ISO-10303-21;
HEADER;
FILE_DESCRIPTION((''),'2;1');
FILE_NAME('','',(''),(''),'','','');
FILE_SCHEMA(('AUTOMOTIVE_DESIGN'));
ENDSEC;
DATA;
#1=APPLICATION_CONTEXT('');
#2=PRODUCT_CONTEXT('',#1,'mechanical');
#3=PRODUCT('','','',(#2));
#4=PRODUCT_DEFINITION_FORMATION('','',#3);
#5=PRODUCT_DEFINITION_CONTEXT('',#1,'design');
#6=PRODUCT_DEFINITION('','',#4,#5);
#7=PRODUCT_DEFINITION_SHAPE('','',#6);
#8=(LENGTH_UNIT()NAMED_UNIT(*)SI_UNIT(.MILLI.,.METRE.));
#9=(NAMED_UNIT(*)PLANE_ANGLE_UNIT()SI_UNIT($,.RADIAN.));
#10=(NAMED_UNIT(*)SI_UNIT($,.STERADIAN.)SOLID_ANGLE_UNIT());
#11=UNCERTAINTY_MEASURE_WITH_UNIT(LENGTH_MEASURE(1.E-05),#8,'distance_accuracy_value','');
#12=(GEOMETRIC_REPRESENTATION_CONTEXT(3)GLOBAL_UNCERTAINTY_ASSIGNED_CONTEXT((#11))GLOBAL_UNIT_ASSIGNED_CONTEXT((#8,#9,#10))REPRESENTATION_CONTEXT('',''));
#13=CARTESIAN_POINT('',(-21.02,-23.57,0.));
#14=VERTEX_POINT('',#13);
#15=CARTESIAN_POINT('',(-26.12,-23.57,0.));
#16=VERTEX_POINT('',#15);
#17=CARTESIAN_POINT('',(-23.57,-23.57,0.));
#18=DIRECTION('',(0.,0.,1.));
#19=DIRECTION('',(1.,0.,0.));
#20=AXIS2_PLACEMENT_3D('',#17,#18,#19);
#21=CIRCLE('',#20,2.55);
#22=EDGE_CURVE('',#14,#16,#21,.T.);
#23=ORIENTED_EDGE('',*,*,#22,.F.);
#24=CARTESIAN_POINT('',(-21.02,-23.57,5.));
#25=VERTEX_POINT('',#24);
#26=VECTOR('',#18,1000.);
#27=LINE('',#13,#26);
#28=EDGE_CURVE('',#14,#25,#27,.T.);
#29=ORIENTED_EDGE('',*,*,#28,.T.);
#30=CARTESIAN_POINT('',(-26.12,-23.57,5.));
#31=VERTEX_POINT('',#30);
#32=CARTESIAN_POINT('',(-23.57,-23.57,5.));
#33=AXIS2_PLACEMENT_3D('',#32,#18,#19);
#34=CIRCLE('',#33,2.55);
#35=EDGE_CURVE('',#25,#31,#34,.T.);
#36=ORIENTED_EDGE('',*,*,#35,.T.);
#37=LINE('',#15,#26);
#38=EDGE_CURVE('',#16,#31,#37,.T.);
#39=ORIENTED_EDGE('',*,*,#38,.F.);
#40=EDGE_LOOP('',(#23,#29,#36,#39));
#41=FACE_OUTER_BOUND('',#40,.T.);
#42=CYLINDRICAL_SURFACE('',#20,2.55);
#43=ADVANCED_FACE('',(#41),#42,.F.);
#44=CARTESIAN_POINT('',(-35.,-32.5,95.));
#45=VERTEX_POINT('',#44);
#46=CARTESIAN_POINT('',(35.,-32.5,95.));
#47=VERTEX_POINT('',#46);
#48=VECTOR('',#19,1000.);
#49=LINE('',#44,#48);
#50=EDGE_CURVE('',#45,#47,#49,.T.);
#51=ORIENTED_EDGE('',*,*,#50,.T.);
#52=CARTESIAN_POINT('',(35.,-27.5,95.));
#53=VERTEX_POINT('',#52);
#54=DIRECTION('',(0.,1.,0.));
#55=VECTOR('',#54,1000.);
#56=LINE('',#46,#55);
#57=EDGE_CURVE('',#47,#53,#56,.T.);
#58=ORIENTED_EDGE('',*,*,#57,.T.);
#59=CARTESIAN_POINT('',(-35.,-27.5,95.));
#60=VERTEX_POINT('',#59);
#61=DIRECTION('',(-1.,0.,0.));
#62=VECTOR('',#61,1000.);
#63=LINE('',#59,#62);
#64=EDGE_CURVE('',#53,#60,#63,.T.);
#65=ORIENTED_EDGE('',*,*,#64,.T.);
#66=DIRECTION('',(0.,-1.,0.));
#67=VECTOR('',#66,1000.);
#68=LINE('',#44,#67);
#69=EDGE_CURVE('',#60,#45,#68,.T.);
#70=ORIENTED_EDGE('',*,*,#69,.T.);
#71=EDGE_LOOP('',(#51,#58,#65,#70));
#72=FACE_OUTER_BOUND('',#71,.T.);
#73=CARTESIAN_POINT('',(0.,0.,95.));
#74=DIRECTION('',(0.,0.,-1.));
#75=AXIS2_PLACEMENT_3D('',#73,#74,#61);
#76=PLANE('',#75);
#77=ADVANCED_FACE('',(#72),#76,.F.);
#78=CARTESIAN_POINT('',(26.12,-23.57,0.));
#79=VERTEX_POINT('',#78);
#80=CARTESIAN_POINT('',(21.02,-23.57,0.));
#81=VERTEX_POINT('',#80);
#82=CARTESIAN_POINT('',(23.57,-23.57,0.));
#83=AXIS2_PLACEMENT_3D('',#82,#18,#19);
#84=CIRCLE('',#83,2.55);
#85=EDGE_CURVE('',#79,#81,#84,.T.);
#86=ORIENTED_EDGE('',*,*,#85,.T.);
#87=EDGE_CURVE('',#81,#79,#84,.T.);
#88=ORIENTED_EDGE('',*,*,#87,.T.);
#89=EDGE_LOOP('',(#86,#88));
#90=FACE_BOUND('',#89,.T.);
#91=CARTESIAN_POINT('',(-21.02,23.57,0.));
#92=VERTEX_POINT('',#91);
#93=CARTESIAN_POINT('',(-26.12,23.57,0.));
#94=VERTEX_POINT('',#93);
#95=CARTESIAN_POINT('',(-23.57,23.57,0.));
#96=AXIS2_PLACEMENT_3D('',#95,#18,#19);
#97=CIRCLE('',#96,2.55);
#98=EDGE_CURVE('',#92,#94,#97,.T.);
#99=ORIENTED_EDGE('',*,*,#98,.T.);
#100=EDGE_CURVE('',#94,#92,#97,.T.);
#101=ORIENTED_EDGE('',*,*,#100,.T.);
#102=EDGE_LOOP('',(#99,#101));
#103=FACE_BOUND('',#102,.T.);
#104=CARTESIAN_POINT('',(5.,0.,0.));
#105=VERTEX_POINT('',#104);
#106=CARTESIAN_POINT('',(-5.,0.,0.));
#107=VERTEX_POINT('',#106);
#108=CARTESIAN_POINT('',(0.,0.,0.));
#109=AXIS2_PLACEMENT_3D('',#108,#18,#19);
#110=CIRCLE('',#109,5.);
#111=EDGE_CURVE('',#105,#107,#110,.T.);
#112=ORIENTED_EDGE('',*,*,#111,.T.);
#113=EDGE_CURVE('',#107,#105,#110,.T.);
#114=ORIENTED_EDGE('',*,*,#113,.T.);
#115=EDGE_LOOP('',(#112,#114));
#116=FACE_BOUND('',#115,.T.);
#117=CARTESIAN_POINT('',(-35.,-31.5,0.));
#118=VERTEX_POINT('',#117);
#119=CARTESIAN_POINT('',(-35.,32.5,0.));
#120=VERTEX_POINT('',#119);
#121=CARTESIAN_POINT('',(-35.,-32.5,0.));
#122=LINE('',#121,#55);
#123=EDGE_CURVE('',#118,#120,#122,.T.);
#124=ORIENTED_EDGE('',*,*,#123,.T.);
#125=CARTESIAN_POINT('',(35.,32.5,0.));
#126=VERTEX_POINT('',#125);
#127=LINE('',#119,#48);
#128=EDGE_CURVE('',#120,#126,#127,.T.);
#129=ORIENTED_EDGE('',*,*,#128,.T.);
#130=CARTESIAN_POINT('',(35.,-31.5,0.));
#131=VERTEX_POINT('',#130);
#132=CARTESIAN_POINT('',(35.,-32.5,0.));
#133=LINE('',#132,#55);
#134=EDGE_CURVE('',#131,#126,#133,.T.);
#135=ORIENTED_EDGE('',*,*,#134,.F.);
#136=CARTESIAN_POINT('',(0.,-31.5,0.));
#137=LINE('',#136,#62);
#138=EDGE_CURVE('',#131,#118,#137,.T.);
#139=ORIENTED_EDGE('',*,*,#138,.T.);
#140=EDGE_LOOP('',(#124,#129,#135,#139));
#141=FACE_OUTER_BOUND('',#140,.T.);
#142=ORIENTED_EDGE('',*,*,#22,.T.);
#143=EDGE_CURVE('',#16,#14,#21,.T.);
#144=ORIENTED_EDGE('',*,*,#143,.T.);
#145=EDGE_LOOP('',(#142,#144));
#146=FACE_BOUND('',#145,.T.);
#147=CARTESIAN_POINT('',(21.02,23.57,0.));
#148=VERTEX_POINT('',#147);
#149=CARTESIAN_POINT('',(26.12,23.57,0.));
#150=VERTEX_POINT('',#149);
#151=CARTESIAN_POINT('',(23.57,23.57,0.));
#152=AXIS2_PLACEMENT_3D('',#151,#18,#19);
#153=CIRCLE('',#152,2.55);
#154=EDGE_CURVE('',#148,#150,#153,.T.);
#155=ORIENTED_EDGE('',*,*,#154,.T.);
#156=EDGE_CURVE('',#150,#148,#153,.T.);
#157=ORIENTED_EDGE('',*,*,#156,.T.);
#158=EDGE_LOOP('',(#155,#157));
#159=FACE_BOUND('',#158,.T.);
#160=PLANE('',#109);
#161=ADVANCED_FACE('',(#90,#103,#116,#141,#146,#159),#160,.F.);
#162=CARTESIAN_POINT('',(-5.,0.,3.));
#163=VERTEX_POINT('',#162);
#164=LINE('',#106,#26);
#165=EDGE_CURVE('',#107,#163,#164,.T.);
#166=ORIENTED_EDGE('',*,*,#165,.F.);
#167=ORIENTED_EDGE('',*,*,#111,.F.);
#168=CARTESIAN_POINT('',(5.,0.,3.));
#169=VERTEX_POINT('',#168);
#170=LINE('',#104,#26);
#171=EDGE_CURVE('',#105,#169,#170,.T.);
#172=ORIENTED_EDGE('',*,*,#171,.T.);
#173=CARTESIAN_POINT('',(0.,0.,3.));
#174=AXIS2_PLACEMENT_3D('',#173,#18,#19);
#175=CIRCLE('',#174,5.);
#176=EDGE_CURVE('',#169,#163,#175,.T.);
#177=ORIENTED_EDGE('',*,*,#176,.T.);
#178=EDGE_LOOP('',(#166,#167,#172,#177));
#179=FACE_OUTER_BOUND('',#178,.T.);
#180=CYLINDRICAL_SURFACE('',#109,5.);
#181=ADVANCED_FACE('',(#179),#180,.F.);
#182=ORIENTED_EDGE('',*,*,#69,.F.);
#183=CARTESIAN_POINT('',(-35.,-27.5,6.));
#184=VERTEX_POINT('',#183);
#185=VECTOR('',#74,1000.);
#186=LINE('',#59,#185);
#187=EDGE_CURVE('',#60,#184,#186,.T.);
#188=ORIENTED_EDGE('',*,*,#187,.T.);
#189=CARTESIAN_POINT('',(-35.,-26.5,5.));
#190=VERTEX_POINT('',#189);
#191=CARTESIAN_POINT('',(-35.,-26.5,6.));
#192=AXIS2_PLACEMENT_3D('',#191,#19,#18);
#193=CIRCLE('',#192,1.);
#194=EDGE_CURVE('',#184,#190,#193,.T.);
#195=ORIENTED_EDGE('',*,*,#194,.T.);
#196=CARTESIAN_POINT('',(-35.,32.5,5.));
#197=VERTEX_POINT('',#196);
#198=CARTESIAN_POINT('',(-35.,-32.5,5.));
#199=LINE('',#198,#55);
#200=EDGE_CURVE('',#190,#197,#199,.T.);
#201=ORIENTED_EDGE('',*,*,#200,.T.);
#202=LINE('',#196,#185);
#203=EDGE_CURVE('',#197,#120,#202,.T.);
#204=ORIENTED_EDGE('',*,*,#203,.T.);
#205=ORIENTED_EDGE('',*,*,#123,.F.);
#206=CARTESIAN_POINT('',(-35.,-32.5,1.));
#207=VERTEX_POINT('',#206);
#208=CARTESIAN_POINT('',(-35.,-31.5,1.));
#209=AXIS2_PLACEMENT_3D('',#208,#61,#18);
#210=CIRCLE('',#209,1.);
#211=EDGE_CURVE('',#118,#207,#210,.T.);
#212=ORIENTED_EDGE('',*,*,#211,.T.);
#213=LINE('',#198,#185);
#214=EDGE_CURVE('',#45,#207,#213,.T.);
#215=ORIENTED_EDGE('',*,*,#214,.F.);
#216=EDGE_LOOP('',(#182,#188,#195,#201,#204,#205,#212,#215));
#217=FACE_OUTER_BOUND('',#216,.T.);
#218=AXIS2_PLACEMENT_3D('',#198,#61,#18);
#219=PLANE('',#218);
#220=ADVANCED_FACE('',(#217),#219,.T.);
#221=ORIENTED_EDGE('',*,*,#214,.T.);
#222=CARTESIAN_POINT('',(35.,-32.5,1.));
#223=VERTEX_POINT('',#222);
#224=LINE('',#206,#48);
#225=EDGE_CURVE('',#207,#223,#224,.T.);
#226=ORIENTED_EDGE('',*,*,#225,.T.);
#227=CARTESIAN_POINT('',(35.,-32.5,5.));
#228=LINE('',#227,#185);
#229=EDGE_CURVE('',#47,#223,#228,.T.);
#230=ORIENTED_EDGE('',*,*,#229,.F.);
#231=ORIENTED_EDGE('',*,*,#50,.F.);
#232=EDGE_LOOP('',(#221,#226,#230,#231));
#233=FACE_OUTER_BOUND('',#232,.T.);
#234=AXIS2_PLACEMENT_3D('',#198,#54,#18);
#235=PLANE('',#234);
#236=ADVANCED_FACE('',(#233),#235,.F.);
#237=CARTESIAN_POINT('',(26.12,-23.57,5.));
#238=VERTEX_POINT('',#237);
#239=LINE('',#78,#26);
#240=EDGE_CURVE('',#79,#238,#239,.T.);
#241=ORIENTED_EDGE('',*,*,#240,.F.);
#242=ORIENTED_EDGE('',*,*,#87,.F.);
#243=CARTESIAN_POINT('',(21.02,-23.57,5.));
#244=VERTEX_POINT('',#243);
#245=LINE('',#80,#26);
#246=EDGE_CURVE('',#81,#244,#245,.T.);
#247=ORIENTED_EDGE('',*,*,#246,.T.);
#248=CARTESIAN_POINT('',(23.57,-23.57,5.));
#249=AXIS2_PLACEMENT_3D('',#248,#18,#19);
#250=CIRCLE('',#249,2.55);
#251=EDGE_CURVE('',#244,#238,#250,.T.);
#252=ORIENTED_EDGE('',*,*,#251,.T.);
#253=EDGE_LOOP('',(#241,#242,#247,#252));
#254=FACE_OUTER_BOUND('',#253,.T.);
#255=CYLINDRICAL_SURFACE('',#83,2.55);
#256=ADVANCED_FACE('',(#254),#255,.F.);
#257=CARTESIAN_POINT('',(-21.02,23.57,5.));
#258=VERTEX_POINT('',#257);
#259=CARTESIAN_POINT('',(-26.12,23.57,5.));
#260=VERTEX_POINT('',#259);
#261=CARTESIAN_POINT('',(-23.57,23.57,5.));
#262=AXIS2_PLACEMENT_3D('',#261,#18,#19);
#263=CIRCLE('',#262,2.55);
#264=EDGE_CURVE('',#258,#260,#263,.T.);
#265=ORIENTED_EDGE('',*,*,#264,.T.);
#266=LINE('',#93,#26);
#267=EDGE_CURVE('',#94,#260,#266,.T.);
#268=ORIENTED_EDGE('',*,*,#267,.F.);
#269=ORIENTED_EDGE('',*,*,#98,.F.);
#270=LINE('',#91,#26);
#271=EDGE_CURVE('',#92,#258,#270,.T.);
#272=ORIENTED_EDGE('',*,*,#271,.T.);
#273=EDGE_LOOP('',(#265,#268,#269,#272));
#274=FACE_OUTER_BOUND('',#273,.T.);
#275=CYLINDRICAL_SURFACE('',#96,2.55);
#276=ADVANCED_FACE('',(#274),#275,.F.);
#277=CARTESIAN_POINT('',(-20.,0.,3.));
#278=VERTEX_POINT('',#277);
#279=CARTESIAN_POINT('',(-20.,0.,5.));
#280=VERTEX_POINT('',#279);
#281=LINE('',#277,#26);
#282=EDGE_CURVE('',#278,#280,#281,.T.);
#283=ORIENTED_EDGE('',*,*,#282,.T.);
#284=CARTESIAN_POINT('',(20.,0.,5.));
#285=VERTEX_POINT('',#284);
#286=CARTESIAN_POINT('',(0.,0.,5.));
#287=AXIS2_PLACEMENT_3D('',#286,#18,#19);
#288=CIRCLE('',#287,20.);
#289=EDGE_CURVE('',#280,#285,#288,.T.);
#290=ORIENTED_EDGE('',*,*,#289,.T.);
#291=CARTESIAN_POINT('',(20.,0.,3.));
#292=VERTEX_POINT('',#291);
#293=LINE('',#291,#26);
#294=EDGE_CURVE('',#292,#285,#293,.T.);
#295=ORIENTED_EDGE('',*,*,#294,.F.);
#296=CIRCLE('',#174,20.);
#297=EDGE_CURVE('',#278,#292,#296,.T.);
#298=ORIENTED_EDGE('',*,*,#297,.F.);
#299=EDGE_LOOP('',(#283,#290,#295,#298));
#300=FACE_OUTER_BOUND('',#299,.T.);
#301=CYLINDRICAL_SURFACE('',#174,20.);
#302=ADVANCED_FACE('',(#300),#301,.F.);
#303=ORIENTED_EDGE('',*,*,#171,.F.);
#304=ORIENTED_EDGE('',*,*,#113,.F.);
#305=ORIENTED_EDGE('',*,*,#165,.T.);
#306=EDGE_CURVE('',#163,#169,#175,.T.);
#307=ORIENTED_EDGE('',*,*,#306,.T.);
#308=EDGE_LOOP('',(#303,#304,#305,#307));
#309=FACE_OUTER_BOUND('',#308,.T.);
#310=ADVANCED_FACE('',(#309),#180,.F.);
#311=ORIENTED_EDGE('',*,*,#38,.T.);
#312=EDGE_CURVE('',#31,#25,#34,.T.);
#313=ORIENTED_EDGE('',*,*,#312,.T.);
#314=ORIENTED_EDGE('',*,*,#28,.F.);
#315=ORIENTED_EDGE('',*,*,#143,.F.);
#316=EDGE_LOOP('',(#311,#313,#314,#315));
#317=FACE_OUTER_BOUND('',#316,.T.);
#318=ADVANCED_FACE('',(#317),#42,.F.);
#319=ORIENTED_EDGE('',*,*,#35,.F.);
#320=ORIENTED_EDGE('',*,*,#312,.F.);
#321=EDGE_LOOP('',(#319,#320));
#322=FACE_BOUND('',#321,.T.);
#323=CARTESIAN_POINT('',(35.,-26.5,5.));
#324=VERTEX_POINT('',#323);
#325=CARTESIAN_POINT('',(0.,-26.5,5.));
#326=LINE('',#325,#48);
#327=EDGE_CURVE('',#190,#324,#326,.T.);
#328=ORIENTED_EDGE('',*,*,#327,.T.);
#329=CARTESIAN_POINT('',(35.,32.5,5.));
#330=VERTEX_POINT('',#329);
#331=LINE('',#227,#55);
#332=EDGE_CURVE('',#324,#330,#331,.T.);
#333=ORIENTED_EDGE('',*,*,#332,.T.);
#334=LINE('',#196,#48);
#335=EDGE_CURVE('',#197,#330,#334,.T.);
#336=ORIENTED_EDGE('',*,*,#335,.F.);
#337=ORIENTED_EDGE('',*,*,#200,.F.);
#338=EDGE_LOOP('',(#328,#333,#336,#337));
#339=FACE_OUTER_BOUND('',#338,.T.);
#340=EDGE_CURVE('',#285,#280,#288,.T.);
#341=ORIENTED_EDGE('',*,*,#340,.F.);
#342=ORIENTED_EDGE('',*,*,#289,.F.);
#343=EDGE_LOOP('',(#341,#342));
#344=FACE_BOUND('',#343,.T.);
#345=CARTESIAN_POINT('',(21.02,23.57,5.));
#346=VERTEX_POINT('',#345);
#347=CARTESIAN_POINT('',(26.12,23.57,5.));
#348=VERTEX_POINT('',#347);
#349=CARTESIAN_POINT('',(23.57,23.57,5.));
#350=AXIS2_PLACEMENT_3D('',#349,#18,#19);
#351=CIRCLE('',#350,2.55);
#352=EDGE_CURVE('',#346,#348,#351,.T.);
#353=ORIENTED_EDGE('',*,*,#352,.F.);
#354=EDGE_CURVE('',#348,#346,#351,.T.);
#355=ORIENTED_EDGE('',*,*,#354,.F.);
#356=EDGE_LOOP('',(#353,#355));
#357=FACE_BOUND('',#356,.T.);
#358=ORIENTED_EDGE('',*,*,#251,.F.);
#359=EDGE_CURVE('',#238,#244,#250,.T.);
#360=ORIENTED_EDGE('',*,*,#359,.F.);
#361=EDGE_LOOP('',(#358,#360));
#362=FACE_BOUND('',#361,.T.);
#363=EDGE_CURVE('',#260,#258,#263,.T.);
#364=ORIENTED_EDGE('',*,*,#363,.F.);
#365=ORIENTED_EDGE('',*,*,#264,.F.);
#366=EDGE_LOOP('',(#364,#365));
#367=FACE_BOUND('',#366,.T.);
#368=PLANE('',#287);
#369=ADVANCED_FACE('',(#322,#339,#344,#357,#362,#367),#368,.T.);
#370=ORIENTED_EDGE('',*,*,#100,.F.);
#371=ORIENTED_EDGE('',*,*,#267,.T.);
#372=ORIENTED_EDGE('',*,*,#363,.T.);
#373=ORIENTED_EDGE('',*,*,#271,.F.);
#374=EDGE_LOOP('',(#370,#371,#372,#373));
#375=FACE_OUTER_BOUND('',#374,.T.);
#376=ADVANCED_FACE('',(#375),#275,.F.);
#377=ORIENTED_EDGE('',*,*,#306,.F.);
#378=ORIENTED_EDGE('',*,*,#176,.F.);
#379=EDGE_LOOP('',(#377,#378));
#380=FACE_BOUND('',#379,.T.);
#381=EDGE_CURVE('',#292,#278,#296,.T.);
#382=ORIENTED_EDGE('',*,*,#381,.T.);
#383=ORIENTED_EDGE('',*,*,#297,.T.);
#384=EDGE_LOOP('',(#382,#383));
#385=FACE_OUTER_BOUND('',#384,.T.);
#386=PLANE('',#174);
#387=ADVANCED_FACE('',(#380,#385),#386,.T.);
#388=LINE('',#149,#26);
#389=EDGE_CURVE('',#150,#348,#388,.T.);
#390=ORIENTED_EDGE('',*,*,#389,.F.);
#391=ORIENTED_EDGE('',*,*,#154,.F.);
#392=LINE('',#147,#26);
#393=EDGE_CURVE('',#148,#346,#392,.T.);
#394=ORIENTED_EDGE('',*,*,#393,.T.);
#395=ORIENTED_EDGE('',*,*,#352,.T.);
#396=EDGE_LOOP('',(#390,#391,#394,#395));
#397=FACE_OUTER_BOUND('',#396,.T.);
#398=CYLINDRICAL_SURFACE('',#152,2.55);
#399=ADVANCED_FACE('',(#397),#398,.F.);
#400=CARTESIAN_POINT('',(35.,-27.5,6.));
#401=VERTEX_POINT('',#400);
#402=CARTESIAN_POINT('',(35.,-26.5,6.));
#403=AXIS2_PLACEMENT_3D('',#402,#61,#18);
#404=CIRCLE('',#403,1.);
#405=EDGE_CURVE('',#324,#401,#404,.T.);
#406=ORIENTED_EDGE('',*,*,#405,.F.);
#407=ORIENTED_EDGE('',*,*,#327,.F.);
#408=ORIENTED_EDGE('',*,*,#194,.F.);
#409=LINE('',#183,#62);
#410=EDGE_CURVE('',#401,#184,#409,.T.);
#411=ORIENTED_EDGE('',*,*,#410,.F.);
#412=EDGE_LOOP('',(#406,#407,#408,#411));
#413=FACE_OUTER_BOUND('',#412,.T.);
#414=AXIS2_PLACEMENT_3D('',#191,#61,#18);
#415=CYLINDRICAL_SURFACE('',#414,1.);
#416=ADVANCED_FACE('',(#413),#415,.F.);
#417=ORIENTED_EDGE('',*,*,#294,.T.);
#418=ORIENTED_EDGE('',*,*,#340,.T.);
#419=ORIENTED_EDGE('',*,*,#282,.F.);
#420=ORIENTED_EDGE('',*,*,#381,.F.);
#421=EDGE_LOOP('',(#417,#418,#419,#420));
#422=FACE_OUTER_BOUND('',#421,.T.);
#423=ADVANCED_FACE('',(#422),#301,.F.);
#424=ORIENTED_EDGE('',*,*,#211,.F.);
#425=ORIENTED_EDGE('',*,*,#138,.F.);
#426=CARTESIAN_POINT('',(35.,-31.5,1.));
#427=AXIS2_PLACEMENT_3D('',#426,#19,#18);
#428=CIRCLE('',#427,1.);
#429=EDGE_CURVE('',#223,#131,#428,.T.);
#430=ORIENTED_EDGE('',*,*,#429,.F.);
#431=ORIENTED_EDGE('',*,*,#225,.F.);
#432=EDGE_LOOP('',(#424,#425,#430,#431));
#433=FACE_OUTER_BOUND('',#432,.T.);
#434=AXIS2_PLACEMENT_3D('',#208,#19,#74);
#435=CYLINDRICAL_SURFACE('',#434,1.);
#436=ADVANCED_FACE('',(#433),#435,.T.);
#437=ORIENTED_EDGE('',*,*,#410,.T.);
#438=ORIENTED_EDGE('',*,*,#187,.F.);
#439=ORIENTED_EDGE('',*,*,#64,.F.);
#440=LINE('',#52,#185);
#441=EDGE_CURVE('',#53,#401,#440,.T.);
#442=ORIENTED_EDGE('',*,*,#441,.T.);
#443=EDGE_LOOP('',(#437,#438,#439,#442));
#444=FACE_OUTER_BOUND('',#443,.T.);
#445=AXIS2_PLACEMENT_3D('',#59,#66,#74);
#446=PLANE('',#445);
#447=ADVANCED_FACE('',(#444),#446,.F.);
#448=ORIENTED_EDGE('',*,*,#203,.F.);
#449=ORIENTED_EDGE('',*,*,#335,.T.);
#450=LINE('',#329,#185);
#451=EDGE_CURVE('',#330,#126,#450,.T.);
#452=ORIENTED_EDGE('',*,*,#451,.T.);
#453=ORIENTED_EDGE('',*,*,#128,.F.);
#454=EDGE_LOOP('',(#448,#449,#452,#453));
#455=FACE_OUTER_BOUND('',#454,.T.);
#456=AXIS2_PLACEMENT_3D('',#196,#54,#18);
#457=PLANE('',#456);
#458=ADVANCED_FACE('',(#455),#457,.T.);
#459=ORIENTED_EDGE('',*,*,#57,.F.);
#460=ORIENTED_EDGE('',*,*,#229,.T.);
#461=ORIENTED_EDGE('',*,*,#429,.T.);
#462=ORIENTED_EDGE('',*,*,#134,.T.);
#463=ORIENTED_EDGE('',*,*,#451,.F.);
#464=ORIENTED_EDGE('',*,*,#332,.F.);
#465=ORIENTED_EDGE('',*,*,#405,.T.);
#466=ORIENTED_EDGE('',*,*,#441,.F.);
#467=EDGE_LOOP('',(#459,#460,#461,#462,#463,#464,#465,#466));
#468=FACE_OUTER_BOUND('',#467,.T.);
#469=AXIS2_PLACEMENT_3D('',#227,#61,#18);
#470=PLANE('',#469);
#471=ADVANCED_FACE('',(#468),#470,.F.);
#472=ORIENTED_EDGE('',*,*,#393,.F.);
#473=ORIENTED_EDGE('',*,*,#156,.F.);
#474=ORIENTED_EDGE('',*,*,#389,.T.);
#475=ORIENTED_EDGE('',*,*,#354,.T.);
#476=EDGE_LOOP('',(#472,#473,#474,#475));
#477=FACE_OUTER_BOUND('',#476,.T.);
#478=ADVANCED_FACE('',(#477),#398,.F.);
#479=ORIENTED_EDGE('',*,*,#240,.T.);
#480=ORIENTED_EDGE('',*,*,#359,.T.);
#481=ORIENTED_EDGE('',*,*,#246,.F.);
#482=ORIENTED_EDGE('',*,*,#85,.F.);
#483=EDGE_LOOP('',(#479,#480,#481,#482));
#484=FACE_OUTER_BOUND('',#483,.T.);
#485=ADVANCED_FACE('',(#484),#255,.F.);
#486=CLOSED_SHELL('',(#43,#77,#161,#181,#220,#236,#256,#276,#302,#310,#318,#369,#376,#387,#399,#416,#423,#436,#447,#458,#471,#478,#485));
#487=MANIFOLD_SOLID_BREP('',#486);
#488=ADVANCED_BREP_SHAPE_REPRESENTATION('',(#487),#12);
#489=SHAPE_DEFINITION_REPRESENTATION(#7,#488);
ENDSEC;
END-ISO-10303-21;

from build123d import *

# Parameters (mm, degrees)
SKETCH_1_W               = 70
SKETCH_1_H               = 65
EXTRUDE_1_DEPTH          = 5
CUT_EXTRUDE_2_DEPTH      = 49.023431781
CUT_EXTRUDE_2_DEPTH_BACK = 49.023431781
SKETCH_3_R               = 2.55
SKETCH_4_W               = 70
SKETCH_4_H               = 5
EXTRUDE_2_DEPTH          = 90
FILLET_1_R               = 1
FILLET_2_R               = 1
CUT_EXTRUDE_START        = -5
SKETCH_5_R               = 20
CUT_EXTRUDE_3_DEPTH      = 2
CUT_EXTRUDE_4_DEPTH      = 104.659297702
CUT_EXTRUDE_4_DEPTH_BACK = 104.659297702
SKETCH_6_R               = 5


with BuildPart() as part:
    # 草图1 → 凸台-拉伸1 (new body)
    with BuildSketch(Plane.XY):
        Rectangle(SKETCH_1_W, SKETCH_1_H)
    extrude(amount=EXTRUDE_1_DEPTH)

    # 草图3 → 切除-拉伸2 (cut, two sides: drawn at the far end of the back side and taken through both)
    with BuildSketch(Plane.XY.offset(5).offset(-CUT_EXTRUDE_2_DEPTH_BACK)):
        with Locations((-23.57, 23.57)):
            Circle(SKETCH_3_R)
        with Locations((23.57, 23.57)):
            Circle(SKETCH_3_R)
        with Locations((23.57, -23.57)):
            Circle(SKETCH_3_R)
        with Locations((-23.57, -23.57)):
            Circle(SKETCH_3_R)
    extrude(amount=CUT_EXTRUDE_2_DEPTH + CUT_EXTRUDE_2_DEPTH_BACK, mode=Mode.SUBTRACT)

    # 草图4 → 凸台-拉伸2 (add)
    with BuildSketch(Plane.XY.offset(5)):
        with Locations((0, -30)):
            Rectangle(SKETCH_4_W, SKETCH_4_H)
    extrude(amount=EXTRUDE_2_DEPTH)

    # 圆角1
    fillet_1_edges = [part.edges().sort_by_distance(p)[0] for p in [
        (0, -27.5, 5),
    ]]
    fillet(fillet_1_edges, radius=FILLET_1_R)

    # 圆角2
    fillet_2_edges = [part.edges().sort_by_distance(p)[0] for p in [
        (0, -32.5, 0),
    ]]
    fillet(fillet_2_edges, radius=FILLET_2_R)

    # 草图5 → 切除-拉伸3 (cut)
    with BuildSketch(Plane(origin=(0, 0, 0), x_dir=(-1, 0, 0), z_dir=(0, 0, -1)).offset(CUT_EXTRUDE_START)):
        with Locations(Location((0, 0, 0), (0, 0, 180))):
            Circle(SKETCH_5_R)
    extrude(amount=CUT_EXTRUDE_3_DEPTH, mode=Mode.SUBTRACT)

    # 草图6 → 切除-拉伸4 (cut, two sides: drawn at the far end of the back side and taken through both)
    with BuildSketch(Plane.XY.offset(3).offset(-CUT_EXTRUDE_4_DEPTH_BACK)):
        Circle(SKETCH_6_R)
    extrude(amount=CUT_EXTRUDE_4_DEPTH + CUT_EXTRUDE_4_DEPTH_BACK, mode=Mode.SUBTRACT)


solid = part.part
